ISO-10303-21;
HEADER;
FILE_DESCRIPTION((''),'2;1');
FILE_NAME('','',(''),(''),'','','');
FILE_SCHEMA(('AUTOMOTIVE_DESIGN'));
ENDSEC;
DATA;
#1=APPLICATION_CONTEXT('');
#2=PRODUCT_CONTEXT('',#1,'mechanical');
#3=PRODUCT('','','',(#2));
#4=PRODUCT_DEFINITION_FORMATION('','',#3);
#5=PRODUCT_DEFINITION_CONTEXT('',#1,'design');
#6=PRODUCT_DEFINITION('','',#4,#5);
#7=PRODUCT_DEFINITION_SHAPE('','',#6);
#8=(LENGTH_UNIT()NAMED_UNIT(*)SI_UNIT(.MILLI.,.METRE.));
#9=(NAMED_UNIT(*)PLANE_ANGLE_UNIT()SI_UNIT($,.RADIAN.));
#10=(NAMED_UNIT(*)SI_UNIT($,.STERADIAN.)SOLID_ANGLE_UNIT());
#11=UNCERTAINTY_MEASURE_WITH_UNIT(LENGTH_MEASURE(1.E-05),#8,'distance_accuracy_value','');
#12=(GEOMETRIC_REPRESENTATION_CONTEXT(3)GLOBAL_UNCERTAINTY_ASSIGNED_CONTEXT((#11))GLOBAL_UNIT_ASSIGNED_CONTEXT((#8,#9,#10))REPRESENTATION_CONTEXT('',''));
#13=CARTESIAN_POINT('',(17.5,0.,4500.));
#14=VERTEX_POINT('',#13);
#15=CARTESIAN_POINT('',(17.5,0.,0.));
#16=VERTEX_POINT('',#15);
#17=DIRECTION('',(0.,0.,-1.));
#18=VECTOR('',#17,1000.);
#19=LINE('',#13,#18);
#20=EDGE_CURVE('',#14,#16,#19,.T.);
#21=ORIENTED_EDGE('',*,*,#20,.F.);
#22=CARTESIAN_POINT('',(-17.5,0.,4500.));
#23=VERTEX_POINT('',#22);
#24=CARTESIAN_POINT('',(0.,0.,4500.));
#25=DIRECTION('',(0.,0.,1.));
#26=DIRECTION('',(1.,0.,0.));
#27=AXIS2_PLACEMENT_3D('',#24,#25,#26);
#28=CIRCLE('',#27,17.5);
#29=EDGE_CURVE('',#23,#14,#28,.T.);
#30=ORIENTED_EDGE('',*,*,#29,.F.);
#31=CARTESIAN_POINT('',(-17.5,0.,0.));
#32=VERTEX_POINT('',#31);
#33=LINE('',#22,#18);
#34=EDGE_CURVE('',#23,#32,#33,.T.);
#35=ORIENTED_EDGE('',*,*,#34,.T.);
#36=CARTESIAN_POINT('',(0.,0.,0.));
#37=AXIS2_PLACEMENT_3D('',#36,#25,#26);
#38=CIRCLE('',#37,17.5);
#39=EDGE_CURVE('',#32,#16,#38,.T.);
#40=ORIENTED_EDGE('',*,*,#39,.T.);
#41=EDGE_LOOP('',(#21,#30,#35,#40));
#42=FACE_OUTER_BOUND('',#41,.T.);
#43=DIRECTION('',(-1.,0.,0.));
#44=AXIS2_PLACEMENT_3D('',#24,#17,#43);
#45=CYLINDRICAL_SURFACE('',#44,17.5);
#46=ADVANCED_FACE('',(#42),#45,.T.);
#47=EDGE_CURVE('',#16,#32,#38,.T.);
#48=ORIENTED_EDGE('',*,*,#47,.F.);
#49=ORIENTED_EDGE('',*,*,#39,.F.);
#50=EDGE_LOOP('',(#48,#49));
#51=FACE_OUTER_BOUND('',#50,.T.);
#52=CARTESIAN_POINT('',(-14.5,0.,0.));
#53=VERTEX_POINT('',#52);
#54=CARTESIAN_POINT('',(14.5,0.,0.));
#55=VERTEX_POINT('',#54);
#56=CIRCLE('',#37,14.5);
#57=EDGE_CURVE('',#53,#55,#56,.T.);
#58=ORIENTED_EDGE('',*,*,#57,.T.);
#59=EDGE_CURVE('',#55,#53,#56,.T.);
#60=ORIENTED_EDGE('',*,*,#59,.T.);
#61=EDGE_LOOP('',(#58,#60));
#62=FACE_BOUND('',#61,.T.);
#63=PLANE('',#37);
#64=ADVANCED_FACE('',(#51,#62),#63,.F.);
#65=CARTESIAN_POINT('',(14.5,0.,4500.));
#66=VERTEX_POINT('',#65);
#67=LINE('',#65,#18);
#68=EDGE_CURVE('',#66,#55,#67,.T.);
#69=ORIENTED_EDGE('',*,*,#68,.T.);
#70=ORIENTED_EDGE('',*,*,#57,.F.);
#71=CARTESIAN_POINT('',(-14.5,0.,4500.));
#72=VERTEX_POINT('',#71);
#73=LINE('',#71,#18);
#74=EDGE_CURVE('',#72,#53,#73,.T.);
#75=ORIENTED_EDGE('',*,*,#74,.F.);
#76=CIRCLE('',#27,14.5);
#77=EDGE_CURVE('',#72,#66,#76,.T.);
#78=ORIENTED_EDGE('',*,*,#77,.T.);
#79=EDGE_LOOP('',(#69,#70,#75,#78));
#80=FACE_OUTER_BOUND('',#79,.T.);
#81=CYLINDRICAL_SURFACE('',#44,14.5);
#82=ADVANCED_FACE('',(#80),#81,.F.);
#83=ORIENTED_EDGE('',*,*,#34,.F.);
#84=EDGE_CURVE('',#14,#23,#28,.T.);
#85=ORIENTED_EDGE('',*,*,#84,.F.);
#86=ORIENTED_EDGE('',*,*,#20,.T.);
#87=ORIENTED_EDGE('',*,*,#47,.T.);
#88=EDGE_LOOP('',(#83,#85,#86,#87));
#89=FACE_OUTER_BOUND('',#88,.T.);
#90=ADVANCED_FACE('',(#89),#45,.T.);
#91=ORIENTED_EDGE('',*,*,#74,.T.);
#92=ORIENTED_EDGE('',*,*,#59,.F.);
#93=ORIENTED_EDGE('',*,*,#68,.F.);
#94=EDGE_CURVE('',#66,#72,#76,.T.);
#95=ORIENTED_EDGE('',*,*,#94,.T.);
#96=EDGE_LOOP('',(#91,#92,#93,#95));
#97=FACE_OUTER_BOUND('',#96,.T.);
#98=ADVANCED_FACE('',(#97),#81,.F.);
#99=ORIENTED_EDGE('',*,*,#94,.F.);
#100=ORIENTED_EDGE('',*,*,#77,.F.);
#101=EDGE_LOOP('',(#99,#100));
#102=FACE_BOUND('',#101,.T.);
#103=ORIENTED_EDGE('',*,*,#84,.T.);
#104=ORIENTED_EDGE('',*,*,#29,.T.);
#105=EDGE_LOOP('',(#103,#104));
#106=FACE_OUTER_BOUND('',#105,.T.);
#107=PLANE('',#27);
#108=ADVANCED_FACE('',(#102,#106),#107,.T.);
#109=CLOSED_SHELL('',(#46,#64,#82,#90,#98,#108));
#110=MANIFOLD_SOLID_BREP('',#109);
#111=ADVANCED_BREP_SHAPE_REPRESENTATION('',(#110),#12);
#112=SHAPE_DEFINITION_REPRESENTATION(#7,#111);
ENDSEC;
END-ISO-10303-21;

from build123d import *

# Parameters (mm, degrees)
SKETCH1_R           = 17.5
SKETCH1_R_2         = 14.5
BOSS_EXTRUDE1_DEPTH = 4500


with BuildPart() as part:
    # Sketch1 → Boss-Extrude1 (new body)
    with BuildSketch(Plane.XY):
        Circle(SKETCH1_R)
        Circle(SKETCH1_R_2, mode=Mode.SUBTRACT)
    extrude(amount=BOSS_EXTRUDE1_DEPTH)


solid = part.part
